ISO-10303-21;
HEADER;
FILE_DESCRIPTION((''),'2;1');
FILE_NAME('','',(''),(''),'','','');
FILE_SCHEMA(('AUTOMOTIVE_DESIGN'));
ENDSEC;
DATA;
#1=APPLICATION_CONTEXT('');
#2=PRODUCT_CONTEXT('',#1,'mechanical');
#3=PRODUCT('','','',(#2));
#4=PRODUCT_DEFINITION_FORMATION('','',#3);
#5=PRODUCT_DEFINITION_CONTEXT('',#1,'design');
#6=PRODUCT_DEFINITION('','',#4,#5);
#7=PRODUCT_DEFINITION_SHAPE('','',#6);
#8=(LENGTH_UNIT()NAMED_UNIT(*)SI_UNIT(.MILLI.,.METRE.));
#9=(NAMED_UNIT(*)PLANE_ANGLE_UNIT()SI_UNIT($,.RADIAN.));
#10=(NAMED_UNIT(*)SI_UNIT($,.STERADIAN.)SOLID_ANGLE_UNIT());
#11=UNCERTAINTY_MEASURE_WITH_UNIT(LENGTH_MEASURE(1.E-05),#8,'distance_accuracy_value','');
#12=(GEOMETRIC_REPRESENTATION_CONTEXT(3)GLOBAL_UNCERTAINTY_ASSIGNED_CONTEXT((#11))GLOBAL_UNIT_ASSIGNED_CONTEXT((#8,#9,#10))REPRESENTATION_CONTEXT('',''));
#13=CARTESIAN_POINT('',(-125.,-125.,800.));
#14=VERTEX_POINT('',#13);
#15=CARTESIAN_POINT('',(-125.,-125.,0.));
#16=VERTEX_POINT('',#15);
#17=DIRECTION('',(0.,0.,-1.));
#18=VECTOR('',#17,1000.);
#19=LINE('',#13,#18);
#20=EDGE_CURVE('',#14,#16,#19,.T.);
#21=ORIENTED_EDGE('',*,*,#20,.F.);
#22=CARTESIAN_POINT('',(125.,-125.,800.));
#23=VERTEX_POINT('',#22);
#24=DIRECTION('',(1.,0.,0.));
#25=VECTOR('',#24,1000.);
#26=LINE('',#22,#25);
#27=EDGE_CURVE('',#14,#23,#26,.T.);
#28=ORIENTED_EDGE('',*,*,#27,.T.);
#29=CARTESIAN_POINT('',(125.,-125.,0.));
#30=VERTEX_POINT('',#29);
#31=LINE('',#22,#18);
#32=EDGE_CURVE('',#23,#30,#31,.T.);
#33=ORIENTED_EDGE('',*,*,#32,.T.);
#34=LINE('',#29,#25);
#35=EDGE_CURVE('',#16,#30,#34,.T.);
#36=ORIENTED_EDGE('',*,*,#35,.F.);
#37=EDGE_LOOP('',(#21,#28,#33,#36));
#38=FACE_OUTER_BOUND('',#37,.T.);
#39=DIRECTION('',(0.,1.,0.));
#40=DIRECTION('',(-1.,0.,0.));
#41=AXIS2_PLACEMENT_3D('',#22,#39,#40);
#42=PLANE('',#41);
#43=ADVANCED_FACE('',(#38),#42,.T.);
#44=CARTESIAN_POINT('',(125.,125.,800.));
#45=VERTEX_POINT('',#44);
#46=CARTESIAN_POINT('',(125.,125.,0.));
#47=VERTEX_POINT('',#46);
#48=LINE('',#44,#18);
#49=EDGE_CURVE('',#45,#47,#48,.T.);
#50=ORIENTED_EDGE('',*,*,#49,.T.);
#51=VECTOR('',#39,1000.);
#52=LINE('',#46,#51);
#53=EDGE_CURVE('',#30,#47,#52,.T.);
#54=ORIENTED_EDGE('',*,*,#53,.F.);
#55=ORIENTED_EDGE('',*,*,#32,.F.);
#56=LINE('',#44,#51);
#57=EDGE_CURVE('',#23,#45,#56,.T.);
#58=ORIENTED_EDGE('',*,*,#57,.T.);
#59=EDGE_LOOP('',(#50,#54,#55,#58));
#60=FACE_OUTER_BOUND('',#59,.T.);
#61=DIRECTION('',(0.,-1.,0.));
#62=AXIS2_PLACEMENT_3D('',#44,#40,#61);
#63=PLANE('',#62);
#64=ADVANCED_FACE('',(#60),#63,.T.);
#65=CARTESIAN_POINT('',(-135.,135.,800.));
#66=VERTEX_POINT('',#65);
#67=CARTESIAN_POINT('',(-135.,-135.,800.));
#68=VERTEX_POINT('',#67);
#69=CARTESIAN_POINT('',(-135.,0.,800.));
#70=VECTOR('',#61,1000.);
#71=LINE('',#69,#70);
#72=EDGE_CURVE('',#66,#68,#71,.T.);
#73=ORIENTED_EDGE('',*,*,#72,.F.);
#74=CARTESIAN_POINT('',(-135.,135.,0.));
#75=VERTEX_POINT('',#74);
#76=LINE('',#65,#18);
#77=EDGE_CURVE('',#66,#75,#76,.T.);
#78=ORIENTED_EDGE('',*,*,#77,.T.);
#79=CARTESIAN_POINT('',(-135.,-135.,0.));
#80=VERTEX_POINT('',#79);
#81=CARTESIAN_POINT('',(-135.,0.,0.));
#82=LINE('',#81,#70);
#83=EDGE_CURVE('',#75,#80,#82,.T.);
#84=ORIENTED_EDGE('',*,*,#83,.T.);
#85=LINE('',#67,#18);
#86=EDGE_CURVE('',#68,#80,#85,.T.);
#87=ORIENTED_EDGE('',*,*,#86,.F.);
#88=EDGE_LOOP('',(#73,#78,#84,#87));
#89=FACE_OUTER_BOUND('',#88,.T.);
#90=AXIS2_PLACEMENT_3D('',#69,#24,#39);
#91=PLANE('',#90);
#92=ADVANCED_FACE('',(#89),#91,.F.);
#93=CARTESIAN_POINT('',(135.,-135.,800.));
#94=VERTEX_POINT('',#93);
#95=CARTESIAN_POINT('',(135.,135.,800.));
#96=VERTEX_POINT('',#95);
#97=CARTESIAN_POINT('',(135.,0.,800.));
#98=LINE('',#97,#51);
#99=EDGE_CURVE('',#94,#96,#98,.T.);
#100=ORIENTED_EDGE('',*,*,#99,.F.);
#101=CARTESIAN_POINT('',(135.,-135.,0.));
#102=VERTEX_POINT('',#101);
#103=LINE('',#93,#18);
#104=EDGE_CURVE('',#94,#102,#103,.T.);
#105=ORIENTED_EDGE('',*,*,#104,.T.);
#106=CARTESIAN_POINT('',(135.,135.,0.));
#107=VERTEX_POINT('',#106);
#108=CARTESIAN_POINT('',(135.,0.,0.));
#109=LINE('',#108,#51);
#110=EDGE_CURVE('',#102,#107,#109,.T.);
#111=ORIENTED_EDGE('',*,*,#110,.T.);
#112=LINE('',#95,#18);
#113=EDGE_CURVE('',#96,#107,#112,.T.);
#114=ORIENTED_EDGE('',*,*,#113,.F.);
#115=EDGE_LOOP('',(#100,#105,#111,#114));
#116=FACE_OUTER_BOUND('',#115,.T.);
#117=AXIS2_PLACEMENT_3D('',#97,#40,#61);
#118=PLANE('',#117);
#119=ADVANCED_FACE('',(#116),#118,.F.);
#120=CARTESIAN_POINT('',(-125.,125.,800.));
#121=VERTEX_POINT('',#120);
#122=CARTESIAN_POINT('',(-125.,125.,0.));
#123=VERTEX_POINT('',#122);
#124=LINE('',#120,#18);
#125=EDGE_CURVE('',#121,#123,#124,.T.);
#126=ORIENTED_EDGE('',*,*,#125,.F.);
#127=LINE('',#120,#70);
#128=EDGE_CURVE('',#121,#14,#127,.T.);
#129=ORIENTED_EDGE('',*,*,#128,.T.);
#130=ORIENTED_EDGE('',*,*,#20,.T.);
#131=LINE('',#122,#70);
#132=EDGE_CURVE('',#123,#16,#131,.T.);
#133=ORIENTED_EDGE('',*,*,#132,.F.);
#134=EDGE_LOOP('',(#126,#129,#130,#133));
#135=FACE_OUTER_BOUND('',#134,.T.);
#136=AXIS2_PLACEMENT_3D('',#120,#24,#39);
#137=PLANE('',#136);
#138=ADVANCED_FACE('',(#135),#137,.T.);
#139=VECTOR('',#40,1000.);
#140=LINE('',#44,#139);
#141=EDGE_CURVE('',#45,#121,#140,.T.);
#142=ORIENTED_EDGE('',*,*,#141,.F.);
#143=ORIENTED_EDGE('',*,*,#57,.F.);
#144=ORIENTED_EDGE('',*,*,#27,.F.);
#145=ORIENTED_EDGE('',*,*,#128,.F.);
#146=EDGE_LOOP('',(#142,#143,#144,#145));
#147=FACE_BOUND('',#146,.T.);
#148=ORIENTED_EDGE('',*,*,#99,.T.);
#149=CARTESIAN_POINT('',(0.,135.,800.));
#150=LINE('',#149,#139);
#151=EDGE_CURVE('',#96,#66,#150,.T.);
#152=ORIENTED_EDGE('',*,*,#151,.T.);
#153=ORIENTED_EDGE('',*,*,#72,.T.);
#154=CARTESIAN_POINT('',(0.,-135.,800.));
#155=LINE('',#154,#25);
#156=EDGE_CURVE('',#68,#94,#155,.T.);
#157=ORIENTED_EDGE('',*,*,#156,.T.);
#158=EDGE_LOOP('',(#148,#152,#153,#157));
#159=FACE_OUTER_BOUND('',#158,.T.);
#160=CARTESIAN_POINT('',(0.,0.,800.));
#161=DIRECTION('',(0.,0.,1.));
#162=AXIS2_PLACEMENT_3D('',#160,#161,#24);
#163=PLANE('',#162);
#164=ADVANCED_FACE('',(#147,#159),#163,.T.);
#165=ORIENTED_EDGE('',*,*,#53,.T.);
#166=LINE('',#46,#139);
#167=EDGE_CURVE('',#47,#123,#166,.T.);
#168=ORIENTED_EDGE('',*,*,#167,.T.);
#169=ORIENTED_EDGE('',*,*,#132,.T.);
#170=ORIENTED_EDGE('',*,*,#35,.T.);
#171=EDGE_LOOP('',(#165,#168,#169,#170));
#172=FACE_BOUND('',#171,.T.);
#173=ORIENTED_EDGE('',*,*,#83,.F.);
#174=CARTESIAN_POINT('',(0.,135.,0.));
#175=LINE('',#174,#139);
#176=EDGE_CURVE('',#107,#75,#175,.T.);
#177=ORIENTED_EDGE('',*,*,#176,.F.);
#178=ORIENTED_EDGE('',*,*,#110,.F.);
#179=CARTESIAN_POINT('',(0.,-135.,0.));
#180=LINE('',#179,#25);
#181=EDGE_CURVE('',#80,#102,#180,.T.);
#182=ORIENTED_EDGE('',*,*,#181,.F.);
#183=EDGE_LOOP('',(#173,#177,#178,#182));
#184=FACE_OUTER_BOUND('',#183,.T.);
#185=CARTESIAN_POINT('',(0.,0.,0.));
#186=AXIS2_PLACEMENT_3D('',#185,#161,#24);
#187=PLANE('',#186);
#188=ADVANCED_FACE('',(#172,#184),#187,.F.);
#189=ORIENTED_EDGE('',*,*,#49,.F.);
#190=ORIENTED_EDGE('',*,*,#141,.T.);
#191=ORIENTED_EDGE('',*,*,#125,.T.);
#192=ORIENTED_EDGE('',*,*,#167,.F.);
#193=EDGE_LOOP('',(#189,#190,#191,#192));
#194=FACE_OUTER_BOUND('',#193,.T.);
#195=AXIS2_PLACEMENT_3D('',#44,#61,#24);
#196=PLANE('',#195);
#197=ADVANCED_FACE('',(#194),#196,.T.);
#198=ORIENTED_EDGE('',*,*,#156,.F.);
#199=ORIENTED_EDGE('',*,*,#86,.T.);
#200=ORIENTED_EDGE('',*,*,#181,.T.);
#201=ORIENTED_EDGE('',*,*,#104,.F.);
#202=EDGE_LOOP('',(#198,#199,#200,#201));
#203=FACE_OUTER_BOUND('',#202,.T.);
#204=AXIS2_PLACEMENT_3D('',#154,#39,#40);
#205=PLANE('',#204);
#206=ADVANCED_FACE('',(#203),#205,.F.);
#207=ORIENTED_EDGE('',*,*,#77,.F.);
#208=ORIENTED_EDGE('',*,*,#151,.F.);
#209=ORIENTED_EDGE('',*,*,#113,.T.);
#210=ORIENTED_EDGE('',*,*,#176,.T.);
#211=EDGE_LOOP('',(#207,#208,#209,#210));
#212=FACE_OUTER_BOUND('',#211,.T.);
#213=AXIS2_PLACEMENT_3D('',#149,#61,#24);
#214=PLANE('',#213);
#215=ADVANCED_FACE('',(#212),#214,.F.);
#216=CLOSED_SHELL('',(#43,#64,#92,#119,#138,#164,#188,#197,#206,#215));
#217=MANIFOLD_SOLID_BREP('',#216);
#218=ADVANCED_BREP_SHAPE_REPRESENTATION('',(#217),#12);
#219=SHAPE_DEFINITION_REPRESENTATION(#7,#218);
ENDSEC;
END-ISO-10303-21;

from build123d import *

# Parameters (mm, degrees)
SKETCH1_W           = 270
SKETCH1_H           = 270
SKETCH1_W_2         = 250
SKETCH1_H_2         = 250
EXTRUDE_THIN1_DEPTH = 800


with BuildPart() as part:
    # Sketch1 → Extrude-Thin1 (new body)
    with BuildSketch(Plane.XY):
        Rectangle(SKETCH1_W, SKETCH1_H)
        Rectangle(SKETCH1_W_2, SKETCH1_H_2, mode=Mode.SUBTRACT)
    extrude(amount=EXTRUDE_THIN1_DEPTH)


solid = part.part
